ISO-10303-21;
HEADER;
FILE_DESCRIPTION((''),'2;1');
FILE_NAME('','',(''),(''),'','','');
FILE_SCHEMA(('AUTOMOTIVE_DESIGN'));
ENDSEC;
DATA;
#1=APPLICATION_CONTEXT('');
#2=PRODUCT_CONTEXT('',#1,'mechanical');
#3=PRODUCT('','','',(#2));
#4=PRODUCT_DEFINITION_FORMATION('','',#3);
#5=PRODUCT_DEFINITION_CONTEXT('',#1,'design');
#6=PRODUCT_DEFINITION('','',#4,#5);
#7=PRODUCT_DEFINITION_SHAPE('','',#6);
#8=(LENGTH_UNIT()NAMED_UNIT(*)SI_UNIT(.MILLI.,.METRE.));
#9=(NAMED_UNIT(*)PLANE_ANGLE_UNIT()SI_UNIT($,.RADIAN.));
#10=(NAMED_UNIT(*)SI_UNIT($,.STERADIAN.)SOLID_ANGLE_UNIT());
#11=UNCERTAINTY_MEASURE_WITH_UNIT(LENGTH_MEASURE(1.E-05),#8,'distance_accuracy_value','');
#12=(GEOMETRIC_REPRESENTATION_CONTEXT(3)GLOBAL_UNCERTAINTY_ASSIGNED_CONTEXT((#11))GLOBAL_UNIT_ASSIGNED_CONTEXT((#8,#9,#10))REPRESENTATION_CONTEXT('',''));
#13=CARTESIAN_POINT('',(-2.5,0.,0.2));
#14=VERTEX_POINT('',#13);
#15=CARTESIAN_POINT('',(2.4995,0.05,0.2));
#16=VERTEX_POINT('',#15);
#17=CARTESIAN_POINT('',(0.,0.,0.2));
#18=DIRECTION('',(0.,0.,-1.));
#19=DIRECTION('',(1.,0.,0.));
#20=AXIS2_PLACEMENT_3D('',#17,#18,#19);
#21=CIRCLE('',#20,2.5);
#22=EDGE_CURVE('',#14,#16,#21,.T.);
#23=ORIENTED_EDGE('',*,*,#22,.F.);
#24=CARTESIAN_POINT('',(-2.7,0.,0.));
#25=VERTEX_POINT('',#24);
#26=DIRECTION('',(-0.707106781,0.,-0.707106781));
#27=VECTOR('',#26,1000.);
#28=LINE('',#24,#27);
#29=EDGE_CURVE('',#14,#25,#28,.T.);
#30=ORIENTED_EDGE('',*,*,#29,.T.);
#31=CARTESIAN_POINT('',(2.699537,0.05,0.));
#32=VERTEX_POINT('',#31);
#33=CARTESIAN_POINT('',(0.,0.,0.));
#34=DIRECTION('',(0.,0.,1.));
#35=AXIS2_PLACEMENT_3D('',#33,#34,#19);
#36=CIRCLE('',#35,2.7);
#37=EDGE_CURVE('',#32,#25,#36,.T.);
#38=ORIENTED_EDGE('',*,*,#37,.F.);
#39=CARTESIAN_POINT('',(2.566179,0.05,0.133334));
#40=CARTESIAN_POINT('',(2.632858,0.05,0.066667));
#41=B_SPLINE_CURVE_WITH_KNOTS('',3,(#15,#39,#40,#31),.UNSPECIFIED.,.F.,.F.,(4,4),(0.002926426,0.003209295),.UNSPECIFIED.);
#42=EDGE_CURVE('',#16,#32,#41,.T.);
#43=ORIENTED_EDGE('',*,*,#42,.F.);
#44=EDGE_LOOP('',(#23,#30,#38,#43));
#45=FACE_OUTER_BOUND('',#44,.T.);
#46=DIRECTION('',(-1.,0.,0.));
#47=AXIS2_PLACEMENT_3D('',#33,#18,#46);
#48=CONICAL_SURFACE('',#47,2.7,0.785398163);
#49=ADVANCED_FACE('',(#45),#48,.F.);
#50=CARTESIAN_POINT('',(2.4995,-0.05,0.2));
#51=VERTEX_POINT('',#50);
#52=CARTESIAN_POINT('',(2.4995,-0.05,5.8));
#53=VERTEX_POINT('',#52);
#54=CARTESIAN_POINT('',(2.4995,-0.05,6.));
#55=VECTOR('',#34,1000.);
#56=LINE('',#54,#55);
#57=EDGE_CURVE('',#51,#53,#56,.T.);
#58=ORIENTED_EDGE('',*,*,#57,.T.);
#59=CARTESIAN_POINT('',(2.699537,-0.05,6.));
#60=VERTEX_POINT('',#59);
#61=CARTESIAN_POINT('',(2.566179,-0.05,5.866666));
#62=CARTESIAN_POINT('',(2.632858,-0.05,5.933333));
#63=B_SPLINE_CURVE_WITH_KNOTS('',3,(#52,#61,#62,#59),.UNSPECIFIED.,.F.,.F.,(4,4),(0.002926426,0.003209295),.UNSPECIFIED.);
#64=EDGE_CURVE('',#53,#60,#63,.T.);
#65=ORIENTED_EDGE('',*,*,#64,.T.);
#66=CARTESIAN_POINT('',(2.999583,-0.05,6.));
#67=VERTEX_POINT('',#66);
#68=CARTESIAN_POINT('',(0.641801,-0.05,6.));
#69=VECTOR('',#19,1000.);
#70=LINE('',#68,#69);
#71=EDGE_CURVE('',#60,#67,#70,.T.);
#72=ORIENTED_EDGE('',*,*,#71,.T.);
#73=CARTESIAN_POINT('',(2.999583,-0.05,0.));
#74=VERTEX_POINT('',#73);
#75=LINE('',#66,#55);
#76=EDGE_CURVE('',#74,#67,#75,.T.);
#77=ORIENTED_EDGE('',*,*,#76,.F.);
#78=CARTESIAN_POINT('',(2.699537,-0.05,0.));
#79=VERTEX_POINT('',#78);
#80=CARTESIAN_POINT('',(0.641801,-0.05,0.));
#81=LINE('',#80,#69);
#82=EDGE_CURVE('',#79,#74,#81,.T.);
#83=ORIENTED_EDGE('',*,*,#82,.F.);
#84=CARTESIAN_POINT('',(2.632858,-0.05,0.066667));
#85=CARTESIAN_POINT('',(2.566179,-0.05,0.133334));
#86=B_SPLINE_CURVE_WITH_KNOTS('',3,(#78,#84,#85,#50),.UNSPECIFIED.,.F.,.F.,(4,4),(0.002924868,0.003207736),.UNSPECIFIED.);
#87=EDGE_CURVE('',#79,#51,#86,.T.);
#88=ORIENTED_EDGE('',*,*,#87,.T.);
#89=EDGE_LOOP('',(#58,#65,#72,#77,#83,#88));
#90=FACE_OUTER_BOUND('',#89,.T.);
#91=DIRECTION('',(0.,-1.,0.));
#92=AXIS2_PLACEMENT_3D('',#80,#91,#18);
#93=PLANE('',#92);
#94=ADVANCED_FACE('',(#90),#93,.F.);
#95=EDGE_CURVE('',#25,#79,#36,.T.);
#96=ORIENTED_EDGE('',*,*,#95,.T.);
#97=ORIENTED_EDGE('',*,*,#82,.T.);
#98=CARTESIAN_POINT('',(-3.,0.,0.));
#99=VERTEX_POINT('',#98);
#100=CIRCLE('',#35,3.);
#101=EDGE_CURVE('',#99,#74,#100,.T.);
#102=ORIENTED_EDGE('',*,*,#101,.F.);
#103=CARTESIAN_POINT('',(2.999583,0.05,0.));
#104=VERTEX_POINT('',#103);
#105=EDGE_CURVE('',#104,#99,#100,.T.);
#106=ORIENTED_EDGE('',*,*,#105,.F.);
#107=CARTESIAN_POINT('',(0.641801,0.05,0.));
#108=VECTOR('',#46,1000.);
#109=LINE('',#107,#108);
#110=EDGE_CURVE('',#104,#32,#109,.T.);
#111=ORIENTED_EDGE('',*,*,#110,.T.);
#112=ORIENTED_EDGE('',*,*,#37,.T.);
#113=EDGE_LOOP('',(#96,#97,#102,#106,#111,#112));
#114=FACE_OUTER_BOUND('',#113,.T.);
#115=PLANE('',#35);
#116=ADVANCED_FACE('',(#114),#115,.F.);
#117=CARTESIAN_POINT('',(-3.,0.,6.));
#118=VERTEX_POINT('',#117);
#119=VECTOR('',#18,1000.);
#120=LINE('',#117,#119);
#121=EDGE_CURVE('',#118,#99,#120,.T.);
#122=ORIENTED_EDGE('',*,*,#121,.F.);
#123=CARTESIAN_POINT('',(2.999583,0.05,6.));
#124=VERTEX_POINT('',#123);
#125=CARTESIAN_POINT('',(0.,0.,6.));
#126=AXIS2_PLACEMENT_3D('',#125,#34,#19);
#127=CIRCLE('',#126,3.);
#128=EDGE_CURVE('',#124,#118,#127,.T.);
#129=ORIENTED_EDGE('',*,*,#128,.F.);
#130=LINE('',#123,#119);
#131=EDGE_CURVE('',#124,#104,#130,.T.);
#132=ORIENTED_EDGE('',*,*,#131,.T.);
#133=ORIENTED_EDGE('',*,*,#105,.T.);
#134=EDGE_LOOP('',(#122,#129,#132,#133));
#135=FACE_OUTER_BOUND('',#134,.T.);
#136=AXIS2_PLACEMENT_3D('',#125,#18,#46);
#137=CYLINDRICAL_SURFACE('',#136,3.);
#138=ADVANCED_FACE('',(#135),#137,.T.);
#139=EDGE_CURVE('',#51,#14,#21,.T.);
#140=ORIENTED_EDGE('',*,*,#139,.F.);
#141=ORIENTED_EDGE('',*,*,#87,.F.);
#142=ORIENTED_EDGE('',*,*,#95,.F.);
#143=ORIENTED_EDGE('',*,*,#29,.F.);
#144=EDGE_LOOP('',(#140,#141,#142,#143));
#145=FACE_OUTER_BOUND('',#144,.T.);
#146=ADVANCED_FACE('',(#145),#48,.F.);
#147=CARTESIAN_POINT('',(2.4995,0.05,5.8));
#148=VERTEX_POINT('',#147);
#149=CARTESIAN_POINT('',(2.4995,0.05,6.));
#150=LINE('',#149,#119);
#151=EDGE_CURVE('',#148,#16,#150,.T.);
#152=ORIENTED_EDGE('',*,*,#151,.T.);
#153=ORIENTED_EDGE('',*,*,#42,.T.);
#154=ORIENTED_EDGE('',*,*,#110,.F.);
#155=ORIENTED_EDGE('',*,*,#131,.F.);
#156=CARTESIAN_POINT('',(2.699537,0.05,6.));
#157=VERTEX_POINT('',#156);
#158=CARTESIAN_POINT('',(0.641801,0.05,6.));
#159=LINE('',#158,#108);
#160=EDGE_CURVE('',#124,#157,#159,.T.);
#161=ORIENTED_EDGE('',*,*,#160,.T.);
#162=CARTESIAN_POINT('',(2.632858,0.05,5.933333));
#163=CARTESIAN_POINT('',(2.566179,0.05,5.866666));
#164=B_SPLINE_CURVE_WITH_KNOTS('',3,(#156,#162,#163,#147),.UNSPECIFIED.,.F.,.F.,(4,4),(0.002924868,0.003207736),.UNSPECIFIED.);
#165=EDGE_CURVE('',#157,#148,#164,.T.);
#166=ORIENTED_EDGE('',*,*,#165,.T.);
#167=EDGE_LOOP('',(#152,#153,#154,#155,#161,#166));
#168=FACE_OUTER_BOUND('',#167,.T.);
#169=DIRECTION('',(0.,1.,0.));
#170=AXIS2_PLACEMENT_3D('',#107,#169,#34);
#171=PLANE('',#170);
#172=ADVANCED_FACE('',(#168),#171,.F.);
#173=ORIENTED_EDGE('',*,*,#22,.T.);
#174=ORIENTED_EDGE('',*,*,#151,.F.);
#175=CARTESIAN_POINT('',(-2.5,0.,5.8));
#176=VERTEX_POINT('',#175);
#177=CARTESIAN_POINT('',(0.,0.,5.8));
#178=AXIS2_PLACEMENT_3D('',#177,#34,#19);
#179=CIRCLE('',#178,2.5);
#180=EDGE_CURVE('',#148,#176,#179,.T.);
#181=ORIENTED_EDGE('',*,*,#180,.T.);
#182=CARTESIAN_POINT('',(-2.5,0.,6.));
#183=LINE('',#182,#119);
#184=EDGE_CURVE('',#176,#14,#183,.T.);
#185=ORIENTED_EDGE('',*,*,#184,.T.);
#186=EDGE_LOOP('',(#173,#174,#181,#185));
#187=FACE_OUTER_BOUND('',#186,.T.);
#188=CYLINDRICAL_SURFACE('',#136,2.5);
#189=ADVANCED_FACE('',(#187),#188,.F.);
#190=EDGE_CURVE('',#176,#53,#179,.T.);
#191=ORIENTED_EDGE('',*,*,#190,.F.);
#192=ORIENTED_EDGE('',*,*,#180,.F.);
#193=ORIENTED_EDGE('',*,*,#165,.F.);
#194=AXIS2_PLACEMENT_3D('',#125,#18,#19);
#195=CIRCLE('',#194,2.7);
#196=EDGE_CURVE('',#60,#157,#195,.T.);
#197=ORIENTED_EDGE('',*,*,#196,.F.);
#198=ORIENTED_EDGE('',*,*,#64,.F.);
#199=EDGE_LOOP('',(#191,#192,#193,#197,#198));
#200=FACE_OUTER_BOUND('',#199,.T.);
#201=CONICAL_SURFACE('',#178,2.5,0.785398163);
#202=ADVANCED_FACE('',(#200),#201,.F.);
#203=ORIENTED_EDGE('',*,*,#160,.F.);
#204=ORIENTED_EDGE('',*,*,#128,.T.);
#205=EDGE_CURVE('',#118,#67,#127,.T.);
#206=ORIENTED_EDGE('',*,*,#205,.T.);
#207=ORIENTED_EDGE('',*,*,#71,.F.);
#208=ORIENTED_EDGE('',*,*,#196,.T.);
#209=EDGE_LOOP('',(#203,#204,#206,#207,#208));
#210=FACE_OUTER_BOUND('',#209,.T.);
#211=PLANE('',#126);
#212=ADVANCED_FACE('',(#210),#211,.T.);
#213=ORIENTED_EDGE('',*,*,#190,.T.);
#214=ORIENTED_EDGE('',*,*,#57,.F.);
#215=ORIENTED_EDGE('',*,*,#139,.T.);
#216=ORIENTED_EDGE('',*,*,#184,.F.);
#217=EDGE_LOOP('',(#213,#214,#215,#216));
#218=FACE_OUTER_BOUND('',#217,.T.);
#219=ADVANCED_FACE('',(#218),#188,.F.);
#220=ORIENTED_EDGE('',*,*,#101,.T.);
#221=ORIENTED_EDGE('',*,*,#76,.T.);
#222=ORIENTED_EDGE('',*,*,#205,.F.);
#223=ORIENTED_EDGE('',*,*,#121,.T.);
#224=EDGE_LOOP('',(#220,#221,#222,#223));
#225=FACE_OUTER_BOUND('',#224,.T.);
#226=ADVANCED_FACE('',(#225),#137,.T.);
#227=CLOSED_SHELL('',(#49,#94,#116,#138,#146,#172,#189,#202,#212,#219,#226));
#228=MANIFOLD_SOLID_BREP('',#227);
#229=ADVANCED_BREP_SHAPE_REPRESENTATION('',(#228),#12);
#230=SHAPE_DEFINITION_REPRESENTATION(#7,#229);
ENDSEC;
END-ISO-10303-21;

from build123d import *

# Parameters (mm, degrees)
SKETCH1_R           = 3
SKETCH1_R_2         = 2.5
BOSS_EXTRUDE1_DEPTH = 6
CHAMFER1_SIZE       = 0.2
SKETCH2_W           = 4.716397802
SKETCH2_H           = 0.1
CUT_EXTRUDE1_DEPTH  = 6


with BuildPart() as part:
    # Sketch1 → Boss-Extrude1 (new body)
    with BuildSketch(Plane.XY):
        Circle(SKETCH1_R)
        Circle(SKETCH1_R_2, mode=Mode.SUBTRACT)
    extrude(amount=BOSS_EXTRUDE1_DEPTH)

    # Chamfer1
    chamfer1_edges = [part.edges().sort_by_distance(p)[0] for p in [
        (-2.5, 0, 0),
        (-2.5, 0, 6),
    ]]
    chamfer(chamfer1_edges, length=CHAMFER1_SIZE)

    # Sketch2 → Cut-Extrude1 (cut)
    with BuildSketch(Plane.XY.offset(6)):
        with Locations((3, 0)):
            Rectangle(SKETCH2_W, SKETCH2_H)
    extrude(amount=-CUT_EXTRUDE1_DEPTH, mode=Mode.SUBTRACT)


solid = part.part
